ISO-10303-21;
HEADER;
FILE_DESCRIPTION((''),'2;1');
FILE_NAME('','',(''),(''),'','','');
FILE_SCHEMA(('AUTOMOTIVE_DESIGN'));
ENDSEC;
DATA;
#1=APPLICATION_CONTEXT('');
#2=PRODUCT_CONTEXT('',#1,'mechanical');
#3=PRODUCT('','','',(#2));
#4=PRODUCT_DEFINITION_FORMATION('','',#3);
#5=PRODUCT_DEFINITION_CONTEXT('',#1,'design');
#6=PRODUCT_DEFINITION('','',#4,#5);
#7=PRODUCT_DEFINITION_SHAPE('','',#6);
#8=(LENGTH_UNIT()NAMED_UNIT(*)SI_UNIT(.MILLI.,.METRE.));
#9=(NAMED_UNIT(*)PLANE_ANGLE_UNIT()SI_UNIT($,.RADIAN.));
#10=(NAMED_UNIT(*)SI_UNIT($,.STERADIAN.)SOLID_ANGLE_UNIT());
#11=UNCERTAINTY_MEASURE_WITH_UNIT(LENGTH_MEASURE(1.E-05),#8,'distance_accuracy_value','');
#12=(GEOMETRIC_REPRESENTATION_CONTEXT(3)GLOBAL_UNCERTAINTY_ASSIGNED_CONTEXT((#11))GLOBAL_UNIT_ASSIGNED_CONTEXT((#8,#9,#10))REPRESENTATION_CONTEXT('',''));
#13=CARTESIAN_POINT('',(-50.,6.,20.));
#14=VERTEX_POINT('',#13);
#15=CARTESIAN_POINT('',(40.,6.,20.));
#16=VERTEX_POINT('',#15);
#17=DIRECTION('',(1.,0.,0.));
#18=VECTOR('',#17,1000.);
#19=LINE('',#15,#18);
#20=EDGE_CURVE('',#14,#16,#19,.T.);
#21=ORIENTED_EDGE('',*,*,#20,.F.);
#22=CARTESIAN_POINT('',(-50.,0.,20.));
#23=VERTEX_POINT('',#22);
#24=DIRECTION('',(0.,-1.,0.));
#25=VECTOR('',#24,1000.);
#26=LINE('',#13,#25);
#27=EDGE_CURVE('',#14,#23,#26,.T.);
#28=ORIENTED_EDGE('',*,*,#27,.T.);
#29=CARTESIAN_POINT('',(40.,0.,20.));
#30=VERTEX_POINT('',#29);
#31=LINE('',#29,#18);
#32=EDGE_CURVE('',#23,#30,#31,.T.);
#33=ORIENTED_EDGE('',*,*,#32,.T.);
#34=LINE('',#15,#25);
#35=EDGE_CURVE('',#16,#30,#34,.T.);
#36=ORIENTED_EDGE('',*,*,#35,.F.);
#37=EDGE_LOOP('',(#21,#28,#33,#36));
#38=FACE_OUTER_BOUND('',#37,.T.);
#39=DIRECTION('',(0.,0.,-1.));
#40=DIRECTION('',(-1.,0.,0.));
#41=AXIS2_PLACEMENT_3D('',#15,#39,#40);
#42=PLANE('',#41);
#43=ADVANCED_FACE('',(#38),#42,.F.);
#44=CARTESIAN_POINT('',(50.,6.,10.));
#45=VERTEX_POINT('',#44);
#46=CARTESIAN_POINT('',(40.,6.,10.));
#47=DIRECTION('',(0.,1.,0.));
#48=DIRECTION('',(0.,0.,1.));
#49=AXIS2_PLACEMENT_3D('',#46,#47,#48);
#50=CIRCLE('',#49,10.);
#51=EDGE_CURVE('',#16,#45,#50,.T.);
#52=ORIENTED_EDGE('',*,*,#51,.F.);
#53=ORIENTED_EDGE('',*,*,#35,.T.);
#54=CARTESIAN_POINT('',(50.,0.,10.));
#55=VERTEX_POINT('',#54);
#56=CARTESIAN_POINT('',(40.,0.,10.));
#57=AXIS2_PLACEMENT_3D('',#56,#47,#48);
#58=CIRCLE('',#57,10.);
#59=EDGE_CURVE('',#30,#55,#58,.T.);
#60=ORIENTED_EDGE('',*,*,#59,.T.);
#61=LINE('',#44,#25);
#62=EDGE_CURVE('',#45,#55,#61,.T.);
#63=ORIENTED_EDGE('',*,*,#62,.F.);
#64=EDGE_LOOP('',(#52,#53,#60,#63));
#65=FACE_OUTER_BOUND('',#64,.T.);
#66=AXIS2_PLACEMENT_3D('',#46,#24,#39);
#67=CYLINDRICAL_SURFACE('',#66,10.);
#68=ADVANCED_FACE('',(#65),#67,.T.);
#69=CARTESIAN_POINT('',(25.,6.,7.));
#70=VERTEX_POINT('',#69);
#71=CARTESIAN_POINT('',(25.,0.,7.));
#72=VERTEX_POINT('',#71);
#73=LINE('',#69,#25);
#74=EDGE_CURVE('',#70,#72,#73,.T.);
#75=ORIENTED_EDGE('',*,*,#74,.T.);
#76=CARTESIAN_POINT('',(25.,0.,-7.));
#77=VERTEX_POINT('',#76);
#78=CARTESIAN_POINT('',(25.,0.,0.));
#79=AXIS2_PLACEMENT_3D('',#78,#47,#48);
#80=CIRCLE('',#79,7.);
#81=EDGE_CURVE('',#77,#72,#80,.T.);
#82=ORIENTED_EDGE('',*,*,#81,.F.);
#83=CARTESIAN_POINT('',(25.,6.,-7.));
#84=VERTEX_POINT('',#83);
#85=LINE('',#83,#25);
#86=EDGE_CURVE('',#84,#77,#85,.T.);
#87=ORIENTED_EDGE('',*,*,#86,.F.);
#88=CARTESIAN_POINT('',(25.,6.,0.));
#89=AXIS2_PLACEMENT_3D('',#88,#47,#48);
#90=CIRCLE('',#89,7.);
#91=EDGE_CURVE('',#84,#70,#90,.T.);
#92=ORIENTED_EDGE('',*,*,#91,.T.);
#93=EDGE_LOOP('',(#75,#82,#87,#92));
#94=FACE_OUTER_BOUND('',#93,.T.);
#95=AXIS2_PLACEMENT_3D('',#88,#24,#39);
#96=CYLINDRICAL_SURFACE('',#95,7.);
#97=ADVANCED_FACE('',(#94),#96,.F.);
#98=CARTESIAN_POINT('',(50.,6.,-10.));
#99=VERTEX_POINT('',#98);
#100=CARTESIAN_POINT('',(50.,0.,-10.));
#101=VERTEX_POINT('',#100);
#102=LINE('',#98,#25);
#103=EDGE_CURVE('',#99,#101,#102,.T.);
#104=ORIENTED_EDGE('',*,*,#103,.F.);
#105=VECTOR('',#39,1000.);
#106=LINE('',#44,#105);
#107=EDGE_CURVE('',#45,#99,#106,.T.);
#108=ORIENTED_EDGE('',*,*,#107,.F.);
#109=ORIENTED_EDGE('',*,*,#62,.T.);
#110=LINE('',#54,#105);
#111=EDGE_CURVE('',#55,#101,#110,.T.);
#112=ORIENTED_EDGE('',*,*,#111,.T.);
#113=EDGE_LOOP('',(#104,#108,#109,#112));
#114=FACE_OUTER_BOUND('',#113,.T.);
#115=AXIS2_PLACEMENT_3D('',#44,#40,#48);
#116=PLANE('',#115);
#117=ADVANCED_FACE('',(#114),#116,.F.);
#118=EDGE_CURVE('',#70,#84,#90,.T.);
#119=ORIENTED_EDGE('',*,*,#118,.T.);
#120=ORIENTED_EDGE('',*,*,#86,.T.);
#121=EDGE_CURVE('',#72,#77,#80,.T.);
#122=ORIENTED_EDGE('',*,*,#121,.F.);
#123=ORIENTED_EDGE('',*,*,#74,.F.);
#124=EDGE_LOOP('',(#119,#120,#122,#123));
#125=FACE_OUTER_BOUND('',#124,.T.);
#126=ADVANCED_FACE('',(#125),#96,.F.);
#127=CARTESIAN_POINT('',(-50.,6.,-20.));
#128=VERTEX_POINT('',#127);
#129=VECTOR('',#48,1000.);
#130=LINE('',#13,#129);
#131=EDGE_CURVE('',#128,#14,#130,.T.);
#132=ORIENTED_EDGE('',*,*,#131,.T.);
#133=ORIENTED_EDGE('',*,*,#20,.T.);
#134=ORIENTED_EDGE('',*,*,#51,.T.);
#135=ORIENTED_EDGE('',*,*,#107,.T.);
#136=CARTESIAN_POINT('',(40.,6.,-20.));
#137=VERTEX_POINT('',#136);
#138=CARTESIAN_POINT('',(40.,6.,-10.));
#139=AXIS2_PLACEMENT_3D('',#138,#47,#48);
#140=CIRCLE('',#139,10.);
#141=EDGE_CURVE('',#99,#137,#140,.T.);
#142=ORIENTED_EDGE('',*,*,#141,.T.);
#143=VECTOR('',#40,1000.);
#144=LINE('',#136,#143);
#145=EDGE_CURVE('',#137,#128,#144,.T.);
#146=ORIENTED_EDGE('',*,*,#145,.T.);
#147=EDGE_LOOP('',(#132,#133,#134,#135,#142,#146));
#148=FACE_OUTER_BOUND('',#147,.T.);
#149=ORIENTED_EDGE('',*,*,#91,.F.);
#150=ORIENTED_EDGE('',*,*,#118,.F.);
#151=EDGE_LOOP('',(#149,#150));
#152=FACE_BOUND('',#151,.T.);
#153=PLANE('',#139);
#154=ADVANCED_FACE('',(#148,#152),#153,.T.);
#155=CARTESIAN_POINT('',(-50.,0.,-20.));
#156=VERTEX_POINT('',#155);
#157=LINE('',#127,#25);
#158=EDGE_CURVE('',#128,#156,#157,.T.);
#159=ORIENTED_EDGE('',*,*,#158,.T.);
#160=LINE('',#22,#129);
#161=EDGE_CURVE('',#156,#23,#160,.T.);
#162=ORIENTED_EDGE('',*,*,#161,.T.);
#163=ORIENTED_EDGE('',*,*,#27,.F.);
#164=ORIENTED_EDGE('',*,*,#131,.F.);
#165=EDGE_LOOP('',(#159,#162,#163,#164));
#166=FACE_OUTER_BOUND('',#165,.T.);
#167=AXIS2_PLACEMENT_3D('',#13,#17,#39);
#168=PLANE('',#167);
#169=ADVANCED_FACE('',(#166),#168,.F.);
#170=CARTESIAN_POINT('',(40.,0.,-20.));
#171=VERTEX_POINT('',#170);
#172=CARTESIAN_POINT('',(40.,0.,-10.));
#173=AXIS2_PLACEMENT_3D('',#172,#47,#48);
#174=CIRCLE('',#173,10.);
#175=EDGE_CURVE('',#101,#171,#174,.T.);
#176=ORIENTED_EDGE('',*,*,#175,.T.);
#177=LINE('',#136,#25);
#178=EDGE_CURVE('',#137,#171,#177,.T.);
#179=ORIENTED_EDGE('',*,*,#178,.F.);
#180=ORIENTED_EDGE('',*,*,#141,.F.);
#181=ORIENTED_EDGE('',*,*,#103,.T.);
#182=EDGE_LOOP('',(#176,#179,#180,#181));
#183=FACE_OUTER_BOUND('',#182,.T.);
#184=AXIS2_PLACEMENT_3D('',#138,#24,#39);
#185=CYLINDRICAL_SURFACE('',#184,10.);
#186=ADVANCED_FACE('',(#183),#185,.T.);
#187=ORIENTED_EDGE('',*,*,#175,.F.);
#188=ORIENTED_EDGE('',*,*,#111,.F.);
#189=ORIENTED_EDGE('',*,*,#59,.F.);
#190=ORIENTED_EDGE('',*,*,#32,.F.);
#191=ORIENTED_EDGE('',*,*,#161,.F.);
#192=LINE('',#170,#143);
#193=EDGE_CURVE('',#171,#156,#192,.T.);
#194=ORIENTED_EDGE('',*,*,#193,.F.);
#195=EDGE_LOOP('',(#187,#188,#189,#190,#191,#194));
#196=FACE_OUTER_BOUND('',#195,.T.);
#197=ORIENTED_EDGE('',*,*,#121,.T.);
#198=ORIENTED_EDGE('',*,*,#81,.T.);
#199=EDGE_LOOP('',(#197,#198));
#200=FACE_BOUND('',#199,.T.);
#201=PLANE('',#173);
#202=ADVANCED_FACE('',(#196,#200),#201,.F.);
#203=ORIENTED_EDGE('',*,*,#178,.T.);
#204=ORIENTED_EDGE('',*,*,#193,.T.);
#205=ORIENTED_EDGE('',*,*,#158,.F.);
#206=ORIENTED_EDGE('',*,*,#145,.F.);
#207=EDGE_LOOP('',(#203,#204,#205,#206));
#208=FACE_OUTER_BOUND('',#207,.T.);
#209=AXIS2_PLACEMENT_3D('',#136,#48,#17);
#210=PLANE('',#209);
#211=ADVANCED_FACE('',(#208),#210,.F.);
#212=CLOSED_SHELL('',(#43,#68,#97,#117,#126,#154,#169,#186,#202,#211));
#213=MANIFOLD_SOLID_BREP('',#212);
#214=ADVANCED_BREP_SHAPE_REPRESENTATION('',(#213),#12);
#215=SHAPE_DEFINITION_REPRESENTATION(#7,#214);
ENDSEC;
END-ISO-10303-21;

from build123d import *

# Parameters (mm, degrees)
SKETCH1_R           = 7
BOSS_EXTRUDE1_DEPTH = 6


with BuildPart() as part:
    # Sketch1 → Boss-Extrude1 (new body)
    with BuildSketch(Plane(origin=(0, 0, 0), x_dir=(1, 0, 0), z_dir=(0, 1, 0))):
        with BuildLine():
            Line((40, -20), (-50, -20))
            Line((-50, -20), (-50, 20))
            Line((-50, 20), (40, 20))
            ThreePointArc((40, 20), (47.071067812, 17.071067812), (50, 10))
            Line((50, 10), (50, -10))
            ThreePointArc((50, -10), (47.071067812, -17.071067812), (40, -20))
        make_face()
        with Locations(Location((25, 0, 0), (0, 0, 270))):
            Circle(SKETCH1_R, mode=Mode.SUBTRACT)
    extrude(amount=BOSS_EXTRUDE1_DEPTH)


solid = part.part
